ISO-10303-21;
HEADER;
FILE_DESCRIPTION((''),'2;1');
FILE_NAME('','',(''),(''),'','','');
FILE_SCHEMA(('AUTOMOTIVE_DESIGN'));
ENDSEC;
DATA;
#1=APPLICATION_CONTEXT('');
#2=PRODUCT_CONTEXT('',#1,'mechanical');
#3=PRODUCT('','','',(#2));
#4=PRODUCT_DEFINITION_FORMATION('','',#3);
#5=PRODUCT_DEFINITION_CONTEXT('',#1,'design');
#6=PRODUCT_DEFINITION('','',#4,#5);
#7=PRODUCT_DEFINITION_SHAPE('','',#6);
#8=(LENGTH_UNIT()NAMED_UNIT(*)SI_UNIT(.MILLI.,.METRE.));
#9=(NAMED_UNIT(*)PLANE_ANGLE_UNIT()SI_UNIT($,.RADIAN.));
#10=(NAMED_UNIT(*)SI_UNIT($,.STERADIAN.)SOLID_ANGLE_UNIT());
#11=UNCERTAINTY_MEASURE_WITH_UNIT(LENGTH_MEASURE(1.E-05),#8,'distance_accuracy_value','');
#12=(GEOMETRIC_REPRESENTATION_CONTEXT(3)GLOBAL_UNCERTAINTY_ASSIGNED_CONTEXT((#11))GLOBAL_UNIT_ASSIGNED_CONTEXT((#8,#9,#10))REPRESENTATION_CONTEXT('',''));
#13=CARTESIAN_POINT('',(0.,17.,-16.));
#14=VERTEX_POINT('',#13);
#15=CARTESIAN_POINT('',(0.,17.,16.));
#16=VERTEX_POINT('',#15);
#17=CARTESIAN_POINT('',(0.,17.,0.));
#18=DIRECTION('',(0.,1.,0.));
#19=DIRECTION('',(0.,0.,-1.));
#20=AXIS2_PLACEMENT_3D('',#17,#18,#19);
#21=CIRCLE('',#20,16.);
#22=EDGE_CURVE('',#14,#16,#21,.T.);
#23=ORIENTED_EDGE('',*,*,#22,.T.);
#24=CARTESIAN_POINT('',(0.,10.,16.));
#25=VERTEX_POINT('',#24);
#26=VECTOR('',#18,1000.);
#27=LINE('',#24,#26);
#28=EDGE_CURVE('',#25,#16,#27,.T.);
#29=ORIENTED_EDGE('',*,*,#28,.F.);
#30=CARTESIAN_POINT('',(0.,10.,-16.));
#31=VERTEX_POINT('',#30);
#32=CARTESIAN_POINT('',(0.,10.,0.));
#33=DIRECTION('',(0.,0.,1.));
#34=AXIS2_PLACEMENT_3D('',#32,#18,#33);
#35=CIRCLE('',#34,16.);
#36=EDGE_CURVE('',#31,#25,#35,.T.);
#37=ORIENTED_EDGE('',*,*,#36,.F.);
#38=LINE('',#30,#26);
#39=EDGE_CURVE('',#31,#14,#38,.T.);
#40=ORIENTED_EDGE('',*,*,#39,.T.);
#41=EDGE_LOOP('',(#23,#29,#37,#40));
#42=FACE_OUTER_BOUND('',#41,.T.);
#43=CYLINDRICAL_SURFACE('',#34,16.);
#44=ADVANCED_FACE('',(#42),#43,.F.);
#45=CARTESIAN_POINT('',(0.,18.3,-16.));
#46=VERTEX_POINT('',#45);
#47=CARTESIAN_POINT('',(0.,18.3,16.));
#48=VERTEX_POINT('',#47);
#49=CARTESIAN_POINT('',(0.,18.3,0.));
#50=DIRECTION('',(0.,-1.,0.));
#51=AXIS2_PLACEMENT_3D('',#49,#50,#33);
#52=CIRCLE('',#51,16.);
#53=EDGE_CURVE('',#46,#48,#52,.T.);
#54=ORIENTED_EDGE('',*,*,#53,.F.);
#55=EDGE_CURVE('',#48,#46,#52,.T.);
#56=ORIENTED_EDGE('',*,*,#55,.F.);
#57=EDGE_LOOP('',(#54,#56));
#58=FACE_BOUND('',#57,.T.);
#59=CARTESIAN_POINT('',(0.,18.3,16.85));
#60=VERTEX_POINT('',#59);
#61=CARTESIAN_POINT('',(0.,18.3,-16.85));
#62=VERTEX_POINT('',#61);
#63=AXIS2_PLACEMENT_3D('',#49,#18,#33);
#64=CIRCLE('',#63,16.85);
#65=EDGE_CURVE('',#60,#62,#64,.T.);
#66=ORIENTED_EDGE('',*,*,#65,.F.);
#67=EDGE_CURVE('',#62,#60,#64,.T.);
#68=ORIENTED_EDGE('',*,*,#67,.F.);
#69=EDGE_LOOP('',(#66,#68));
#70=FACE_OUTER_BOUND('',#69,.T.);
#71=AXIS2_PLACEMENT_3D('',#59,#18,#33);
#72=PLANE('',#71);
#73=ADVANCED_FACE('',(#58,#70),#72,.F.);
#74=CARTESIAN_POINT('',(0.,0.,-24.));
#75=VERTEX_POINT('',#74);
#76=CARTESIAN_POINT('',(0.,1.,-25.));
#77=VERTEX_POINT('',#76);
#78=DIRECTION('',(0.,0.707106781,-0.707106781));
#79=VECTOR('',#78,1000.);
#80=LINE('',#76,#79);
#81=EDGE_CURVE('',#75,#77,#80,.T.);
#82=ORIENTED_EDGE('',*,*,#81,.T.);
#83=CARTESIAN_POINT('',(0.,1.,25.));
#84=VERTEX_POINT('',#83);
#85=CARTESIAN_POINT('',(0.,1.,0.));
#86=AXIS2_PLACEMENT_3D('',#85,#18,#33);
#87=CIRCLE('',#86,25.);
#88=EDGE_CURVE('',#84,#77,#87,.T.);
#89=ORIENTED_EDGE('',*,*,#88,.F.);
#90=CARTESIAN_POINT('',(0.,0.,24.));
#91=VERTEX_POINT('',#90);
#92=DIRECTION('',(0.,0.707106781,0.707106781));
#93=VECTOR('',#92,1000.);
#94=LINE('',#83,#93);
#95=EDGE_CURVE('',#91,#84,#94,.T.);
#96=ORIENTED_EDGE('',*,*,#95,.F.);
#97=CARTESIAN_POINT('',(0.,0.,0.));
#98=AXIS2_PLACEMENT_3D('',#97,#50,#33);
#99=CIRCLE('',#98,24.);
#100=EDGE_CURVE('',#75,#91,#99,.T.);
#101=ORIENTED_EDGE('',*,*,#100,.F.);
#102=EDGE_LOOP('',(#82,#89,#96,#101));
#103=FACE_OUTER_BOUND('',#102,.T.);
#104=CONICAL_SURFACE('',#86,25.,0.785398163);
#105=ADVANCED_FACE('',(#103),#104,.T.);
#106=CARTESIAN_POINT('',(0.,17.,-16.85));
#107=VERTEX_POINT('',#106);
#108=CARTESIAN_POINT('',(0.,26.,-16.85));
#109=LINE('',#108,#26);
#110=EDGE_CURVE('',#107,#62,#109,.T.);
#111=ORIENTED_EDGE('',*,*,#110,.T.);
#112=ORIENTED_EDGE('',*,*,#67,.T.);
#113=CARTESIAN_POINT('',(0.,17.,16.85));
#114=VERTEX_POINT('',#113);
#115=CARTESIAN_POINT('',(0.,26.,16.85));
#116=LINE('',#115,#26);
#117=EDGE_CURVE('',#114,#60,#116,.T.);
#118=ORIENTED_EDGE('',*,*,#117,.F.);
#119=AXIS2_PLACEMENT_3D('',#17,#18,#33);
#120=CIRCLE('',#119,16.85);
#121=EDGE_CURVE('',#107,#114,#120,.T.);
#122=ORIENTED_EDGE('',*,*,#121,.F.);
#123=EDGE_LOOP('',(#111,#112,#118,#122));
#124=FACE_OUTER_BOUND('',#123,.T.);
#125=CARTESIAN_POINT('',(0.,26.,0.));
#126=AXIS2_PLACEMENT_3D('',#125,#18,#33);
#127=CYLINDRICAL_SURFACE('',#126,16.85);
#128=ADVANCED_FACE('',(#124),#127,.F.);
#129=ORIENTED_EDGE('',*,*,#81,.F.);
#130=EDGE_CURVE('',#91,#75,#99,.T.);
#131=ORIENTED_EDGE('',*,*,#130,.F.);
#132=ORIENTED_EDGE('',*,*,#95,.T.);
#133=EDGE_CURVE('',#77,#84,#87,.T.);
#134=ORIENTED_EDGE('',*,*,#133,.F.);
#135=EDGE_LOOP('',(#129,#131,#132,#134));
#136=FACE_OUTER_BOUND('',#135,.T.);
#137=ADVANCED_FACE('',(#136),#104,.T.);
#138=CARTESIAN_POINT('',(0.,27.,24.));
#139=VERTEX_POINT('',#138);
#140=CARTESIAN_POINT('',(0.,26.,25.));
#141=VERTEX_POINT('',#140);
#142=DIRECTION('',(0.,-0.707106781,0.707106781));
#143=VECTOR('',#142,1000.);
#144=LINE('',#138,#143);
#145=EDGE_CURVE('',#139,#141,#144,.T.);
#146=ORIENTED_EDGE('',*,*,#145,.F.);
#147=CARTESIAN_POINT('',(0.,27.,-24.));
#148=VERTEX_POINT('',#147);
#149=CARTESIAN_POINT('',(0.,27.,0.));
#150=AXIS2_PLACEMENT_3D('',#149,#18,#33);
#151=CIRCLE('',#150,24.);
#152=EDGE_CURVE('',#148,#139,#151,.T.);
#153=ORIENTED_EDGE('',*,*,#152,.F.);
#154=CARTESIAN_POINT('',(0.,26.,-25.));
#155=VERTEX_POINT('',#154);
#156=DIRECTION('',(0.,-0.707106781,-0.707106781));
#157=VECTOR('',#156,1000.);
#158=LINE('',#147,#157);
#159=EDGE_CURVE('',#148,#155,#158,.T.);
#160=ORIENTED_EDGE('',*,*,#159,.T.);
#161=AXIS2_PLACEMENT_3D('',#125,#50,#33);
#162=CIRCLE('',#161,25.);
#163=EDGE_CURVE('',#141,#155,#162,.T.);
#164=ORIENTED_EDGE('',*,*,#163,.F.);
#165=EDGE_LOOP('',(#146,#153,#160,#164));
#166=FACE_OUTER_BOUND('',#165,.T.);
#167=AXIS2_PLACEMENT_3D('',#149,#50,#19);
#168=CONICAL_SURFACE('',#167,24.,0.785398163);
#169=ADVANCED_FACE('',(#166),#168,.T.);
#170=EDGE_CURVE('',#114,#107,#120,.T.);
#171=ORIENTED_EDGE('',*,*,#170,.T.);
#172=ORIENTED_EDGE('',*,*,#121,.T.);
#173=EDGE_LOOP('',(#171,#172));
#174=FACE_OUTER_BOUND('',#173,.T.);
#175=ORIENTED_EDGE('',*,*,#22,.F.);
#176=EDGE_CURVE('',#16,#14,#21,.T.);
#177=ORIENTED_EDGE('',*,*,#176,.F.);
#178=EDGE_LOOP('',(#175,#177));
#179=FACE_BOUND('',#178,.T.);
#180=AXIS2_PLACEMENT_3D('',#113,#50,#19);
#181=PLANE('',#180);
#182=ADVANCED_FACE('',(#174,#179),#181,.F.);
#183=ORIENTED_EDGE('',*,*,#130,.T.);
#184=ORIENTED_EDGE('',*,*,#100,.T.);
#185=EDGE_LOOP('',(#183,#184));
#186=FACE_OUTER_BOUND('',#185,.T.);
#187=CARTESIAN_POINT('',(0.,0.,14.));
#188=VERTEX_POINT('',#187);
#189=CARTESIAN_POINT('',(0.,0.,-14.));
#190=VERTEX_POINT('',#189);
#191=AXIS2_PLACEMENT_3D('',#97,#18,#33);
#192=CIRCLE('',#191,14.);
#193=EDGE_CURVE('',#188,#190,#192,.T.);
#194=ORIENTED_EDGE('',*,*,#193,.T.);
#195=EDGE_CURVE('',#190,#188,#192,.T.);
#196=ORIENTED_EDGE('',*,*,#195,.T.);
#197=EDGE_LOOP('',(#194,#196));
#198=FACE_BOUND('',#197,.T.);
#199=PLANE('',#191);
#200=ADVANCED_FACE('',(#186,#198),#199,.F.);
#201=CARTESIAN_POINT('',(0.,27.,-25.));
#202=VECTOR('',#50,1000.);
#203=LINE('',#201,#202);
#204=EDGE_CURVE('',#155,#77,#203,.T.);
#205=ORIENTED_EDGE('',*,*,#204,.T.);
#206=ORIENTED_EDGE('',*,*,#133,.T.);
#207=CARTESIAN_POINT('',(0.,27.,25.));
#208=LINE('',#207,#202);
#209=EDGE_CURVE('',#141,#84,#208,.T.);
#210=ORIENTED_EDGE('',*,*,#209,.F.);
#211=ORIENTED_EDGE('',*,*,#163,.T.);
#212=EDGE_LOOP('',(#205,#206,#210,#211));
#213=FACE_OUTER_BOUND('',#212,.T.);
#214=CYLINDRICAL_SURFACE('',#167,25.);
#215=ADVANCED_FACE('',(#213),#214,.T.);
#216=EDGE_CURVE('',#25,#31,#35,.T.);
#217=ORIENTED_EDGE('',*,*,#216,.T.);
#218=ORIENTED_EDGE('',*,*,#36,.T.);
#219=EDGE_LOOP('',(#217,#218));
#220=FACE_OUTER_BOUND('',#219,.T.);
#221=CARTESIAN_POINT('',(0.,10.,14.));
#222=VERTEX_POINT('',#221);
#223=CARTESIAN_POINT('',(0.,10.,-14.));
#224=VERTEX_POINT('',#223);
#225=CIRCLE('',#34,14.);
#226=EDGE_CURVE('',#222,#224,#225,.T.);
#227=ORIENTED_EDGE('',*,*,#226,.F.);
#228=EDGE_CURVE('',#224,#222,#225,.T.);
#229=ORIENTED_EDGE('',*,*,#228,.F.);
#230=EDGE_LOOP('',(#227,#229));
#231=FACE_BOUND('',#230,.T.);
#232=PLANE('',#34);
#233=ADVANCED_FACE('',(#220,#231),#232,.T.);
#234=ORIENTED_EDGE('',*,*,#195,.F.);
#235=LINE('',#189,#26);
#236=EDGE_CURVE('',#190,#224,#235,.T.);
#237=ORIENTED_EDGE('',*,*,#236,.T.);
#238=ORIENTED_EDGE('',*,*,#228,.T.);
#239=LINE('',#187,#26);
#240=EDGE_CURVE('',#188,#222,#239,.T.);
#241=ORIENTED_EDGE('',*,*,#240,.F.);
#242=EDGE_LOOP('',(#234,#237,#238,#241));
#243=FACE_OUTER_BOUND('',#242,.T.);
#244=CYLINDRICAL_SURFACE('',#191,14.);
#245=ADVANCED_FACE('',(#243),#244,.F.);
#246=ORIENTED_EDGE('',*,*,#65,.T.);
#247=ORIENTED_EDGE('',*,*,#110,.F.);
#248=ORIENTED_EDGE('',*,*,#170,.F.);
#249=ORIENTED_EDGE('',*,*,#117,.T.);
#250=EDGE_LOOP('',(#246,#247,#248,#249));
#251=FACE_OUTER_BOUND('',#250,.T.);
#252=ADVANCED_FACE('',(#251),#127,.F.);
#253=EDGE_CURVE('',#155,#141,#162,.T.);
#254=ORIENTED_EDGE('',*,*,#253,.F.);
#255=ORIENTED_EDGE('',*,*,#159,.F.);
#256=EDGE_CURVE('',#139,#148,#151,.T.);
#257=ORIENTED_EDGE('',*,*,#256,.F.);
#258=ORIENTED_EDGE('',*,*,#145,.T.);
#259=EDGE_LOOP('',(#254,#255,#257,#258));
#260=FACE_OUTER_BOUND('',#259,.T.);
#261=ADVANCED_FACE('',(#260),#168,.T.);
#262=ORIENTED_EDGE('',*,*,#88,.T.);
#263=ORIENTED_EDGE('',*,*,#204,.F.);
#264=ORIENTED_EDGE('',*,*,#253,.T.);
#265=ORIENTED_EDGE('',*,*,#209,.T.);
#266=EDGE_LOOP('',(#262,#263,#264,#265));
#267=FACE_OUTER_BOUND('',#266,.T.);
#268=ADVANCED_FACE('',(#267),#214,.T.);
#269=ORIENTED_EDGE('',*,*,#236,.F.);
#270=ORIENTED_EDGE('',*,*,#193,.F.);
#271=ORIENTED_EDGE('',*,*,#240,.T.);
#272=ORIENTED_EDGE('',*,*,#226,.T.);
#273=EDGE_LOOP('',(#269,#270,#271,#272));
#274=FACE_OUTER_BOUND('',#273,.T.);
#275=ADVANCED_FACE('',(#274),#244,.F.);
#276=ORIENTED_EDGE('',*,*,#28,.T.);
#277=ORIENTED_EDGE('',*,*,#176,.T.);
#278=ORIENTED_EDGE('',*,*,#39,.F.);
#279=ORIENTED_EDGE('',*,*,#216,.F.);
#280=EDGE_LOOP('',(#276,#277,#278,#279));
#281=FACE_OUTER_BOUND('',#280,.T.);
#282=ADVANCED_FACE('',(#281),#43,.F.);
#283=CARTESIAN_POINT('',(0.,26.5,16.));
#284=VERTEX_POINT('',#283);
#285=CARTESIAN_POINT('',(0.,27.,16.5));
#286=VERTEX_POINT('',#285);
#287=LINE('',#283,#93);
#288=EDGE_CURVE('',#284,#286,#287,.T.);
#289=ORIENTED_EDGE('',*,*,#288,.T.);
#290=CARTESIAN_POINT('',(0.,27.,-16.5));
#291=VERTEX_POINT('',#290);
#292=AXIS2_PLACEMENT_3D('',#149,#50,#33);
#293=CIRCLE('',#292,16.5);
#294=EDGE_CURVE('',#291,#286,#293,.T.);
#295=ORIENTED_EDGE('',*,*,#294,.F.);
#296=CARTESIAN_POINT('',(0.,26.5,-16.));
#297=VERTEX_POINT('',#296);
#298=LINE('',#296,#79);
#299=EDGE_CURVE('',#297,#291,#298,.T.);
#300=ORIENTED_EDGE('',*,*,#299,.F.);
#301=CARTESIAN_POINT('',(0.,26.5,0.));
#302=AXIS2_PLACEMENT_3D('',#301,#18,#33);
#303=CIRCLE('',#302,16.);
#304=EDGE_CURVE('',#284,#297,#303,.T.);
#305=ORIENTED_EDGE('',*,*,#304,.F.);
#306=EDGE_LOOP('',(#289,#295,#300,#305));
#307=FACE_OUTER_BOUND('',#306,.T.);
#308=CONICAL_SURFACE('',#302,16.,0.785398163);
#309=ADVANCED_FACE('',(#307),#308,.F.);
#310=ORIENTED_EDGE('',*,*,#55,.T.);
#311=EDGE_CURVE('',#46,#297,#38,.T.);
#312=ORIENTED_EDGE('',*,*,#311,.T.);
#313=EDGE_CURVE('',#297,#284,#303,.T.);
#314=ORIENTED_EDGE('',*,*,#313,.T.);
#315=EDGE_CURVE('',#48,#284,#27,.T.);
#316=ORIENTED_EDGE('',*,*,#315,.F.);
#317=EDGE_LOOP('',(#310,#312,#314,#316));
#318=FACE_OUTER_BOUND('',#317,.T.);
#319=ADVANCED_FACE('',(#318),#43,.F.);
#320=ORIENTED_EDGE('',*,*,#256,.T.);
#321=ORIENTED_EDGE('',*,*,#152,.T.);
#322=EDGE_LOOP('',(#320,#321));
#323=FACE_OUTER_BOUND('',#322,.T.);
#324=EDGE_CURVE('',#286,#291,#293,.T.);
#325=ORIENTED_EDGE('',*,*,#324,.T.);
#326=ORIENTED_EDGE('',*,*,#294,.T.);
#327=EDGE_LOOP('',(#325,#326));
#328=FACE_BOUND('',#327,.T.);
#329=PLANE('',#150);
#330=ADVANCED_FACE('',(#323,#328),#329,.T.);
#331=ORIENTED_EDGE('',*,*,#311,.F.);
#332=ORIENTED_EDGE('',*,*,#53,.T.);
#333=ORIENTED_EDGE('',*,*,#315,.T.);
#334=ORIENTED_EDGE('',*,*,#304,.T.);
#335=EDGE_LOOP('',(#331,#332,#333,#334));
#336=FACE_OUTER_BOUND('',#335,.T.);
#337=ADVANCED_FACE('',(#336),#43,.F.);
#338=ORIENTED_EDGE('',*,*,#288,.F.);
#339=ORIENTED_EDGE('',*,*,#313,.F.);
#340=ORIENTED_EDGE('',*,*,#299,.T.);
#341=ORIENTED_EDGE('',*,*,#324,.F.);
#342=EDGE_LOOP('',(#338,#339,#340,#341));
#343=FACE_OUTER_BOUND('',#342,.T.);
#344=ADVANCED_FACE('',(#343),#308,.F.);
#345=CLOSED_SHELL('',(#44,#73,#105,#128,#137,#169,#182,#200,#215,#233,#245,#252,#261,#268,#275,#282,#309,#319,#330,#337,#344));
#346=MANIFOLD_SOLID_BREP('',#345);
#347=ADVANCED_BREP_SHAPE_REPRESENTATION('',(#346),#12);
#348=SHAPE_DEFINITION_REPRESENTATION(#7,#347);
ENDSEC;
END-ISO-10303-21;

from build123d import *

# Parameters (mm, degrees)
SKETCH_1_R          = 25
EXTRUDE_1_DEPTH     = 27
SKETCH_2_R          = 16
CUT_EXTRUDE_1_DEPTH = 17
SKETCH_3_R          = 14
CUT_EXTRUDE_2_DEPTH = 40.230090492
CHAMFER_1_SIZE      = 1
CHAMFER_2_SIZE      = 0.5
SKETCH_4_W          = 2
SKETCH_4_H          = 1.3


with BuildPart() as part:
    # 草图1 → 凸台-拉伸1 (new body)
    with BuildSketch(Plane(origin=(0, 0, 0), x_dir=(1, 0, 0), z_dir=(0, 1, 0))):
        with Locations(Location((0, 0, 0), (0, 0, 270))):
            Circle(SKETCH_1_R)
    extrude(amount=EXTRUDE_1_DEPTH)

    # 草图2 → 切除-拉伸1 (cut)
    with BuildSketch(Plane(origin=(0, 27, 0), x_dir=(1, 0, 0), z_dir=(0, 1, 0))):
        with Locations(Location((0, 0, 0), (0, 0, 270))):
            Circle(SKETCH_2_R)
    extrude(amount=-CUT_EXTRUDE_1_DEPTH, mode=Mode.SUBTRACT)

    # 草图3 → 切除-拉伸2 (cut, through all)
    with BuildSketch(Plane(origin=(0, 10, 0), x_dir=(1, 0, 0), z_dir=(0, 1, 0))):
        with Locations(Location((0, 0, 0), (0, 0, 270))):
            Circle(SKETCH_3_R)
    extrude(amount=-CUT_EXTRUDE_2_DEPTH, mode=Mode.SUBTRACT)

    # 倒角1
    chamfer_1_edges = [part.edges().sort_by_distance(p)[0] for p in [
        (0, 0, -25),
        (0, 27, -25),
    ]]
    chamfer(chamfer_1_edges, length=CHAMFER_1_SIZE)

    # 倒角2
    chamfer_2_edges = [part.edges().sort_by_distance(p)[0] for p in [
        (0, 27, -16),
    ]]
    chamfer(chamfer_2_edges, length=CHAMFER_2_SIZE)

    # 草图4 → 切除-旋转1 (revolve, cut)
    with BuildSketch(Plane(origin=(0, 0, 0), x_dir=(0, 0, -1), z_dir=(1, 0, 0))):
        with Locations((-15.85, 17.65)):
            Rectangle(SKETCH_4_W, SKETCH_4_H)
    revolve(axis=Axis((0, 27, 0), (0, -1, 0)), mode=Mode.SUBTRACT)


solid = part.part
